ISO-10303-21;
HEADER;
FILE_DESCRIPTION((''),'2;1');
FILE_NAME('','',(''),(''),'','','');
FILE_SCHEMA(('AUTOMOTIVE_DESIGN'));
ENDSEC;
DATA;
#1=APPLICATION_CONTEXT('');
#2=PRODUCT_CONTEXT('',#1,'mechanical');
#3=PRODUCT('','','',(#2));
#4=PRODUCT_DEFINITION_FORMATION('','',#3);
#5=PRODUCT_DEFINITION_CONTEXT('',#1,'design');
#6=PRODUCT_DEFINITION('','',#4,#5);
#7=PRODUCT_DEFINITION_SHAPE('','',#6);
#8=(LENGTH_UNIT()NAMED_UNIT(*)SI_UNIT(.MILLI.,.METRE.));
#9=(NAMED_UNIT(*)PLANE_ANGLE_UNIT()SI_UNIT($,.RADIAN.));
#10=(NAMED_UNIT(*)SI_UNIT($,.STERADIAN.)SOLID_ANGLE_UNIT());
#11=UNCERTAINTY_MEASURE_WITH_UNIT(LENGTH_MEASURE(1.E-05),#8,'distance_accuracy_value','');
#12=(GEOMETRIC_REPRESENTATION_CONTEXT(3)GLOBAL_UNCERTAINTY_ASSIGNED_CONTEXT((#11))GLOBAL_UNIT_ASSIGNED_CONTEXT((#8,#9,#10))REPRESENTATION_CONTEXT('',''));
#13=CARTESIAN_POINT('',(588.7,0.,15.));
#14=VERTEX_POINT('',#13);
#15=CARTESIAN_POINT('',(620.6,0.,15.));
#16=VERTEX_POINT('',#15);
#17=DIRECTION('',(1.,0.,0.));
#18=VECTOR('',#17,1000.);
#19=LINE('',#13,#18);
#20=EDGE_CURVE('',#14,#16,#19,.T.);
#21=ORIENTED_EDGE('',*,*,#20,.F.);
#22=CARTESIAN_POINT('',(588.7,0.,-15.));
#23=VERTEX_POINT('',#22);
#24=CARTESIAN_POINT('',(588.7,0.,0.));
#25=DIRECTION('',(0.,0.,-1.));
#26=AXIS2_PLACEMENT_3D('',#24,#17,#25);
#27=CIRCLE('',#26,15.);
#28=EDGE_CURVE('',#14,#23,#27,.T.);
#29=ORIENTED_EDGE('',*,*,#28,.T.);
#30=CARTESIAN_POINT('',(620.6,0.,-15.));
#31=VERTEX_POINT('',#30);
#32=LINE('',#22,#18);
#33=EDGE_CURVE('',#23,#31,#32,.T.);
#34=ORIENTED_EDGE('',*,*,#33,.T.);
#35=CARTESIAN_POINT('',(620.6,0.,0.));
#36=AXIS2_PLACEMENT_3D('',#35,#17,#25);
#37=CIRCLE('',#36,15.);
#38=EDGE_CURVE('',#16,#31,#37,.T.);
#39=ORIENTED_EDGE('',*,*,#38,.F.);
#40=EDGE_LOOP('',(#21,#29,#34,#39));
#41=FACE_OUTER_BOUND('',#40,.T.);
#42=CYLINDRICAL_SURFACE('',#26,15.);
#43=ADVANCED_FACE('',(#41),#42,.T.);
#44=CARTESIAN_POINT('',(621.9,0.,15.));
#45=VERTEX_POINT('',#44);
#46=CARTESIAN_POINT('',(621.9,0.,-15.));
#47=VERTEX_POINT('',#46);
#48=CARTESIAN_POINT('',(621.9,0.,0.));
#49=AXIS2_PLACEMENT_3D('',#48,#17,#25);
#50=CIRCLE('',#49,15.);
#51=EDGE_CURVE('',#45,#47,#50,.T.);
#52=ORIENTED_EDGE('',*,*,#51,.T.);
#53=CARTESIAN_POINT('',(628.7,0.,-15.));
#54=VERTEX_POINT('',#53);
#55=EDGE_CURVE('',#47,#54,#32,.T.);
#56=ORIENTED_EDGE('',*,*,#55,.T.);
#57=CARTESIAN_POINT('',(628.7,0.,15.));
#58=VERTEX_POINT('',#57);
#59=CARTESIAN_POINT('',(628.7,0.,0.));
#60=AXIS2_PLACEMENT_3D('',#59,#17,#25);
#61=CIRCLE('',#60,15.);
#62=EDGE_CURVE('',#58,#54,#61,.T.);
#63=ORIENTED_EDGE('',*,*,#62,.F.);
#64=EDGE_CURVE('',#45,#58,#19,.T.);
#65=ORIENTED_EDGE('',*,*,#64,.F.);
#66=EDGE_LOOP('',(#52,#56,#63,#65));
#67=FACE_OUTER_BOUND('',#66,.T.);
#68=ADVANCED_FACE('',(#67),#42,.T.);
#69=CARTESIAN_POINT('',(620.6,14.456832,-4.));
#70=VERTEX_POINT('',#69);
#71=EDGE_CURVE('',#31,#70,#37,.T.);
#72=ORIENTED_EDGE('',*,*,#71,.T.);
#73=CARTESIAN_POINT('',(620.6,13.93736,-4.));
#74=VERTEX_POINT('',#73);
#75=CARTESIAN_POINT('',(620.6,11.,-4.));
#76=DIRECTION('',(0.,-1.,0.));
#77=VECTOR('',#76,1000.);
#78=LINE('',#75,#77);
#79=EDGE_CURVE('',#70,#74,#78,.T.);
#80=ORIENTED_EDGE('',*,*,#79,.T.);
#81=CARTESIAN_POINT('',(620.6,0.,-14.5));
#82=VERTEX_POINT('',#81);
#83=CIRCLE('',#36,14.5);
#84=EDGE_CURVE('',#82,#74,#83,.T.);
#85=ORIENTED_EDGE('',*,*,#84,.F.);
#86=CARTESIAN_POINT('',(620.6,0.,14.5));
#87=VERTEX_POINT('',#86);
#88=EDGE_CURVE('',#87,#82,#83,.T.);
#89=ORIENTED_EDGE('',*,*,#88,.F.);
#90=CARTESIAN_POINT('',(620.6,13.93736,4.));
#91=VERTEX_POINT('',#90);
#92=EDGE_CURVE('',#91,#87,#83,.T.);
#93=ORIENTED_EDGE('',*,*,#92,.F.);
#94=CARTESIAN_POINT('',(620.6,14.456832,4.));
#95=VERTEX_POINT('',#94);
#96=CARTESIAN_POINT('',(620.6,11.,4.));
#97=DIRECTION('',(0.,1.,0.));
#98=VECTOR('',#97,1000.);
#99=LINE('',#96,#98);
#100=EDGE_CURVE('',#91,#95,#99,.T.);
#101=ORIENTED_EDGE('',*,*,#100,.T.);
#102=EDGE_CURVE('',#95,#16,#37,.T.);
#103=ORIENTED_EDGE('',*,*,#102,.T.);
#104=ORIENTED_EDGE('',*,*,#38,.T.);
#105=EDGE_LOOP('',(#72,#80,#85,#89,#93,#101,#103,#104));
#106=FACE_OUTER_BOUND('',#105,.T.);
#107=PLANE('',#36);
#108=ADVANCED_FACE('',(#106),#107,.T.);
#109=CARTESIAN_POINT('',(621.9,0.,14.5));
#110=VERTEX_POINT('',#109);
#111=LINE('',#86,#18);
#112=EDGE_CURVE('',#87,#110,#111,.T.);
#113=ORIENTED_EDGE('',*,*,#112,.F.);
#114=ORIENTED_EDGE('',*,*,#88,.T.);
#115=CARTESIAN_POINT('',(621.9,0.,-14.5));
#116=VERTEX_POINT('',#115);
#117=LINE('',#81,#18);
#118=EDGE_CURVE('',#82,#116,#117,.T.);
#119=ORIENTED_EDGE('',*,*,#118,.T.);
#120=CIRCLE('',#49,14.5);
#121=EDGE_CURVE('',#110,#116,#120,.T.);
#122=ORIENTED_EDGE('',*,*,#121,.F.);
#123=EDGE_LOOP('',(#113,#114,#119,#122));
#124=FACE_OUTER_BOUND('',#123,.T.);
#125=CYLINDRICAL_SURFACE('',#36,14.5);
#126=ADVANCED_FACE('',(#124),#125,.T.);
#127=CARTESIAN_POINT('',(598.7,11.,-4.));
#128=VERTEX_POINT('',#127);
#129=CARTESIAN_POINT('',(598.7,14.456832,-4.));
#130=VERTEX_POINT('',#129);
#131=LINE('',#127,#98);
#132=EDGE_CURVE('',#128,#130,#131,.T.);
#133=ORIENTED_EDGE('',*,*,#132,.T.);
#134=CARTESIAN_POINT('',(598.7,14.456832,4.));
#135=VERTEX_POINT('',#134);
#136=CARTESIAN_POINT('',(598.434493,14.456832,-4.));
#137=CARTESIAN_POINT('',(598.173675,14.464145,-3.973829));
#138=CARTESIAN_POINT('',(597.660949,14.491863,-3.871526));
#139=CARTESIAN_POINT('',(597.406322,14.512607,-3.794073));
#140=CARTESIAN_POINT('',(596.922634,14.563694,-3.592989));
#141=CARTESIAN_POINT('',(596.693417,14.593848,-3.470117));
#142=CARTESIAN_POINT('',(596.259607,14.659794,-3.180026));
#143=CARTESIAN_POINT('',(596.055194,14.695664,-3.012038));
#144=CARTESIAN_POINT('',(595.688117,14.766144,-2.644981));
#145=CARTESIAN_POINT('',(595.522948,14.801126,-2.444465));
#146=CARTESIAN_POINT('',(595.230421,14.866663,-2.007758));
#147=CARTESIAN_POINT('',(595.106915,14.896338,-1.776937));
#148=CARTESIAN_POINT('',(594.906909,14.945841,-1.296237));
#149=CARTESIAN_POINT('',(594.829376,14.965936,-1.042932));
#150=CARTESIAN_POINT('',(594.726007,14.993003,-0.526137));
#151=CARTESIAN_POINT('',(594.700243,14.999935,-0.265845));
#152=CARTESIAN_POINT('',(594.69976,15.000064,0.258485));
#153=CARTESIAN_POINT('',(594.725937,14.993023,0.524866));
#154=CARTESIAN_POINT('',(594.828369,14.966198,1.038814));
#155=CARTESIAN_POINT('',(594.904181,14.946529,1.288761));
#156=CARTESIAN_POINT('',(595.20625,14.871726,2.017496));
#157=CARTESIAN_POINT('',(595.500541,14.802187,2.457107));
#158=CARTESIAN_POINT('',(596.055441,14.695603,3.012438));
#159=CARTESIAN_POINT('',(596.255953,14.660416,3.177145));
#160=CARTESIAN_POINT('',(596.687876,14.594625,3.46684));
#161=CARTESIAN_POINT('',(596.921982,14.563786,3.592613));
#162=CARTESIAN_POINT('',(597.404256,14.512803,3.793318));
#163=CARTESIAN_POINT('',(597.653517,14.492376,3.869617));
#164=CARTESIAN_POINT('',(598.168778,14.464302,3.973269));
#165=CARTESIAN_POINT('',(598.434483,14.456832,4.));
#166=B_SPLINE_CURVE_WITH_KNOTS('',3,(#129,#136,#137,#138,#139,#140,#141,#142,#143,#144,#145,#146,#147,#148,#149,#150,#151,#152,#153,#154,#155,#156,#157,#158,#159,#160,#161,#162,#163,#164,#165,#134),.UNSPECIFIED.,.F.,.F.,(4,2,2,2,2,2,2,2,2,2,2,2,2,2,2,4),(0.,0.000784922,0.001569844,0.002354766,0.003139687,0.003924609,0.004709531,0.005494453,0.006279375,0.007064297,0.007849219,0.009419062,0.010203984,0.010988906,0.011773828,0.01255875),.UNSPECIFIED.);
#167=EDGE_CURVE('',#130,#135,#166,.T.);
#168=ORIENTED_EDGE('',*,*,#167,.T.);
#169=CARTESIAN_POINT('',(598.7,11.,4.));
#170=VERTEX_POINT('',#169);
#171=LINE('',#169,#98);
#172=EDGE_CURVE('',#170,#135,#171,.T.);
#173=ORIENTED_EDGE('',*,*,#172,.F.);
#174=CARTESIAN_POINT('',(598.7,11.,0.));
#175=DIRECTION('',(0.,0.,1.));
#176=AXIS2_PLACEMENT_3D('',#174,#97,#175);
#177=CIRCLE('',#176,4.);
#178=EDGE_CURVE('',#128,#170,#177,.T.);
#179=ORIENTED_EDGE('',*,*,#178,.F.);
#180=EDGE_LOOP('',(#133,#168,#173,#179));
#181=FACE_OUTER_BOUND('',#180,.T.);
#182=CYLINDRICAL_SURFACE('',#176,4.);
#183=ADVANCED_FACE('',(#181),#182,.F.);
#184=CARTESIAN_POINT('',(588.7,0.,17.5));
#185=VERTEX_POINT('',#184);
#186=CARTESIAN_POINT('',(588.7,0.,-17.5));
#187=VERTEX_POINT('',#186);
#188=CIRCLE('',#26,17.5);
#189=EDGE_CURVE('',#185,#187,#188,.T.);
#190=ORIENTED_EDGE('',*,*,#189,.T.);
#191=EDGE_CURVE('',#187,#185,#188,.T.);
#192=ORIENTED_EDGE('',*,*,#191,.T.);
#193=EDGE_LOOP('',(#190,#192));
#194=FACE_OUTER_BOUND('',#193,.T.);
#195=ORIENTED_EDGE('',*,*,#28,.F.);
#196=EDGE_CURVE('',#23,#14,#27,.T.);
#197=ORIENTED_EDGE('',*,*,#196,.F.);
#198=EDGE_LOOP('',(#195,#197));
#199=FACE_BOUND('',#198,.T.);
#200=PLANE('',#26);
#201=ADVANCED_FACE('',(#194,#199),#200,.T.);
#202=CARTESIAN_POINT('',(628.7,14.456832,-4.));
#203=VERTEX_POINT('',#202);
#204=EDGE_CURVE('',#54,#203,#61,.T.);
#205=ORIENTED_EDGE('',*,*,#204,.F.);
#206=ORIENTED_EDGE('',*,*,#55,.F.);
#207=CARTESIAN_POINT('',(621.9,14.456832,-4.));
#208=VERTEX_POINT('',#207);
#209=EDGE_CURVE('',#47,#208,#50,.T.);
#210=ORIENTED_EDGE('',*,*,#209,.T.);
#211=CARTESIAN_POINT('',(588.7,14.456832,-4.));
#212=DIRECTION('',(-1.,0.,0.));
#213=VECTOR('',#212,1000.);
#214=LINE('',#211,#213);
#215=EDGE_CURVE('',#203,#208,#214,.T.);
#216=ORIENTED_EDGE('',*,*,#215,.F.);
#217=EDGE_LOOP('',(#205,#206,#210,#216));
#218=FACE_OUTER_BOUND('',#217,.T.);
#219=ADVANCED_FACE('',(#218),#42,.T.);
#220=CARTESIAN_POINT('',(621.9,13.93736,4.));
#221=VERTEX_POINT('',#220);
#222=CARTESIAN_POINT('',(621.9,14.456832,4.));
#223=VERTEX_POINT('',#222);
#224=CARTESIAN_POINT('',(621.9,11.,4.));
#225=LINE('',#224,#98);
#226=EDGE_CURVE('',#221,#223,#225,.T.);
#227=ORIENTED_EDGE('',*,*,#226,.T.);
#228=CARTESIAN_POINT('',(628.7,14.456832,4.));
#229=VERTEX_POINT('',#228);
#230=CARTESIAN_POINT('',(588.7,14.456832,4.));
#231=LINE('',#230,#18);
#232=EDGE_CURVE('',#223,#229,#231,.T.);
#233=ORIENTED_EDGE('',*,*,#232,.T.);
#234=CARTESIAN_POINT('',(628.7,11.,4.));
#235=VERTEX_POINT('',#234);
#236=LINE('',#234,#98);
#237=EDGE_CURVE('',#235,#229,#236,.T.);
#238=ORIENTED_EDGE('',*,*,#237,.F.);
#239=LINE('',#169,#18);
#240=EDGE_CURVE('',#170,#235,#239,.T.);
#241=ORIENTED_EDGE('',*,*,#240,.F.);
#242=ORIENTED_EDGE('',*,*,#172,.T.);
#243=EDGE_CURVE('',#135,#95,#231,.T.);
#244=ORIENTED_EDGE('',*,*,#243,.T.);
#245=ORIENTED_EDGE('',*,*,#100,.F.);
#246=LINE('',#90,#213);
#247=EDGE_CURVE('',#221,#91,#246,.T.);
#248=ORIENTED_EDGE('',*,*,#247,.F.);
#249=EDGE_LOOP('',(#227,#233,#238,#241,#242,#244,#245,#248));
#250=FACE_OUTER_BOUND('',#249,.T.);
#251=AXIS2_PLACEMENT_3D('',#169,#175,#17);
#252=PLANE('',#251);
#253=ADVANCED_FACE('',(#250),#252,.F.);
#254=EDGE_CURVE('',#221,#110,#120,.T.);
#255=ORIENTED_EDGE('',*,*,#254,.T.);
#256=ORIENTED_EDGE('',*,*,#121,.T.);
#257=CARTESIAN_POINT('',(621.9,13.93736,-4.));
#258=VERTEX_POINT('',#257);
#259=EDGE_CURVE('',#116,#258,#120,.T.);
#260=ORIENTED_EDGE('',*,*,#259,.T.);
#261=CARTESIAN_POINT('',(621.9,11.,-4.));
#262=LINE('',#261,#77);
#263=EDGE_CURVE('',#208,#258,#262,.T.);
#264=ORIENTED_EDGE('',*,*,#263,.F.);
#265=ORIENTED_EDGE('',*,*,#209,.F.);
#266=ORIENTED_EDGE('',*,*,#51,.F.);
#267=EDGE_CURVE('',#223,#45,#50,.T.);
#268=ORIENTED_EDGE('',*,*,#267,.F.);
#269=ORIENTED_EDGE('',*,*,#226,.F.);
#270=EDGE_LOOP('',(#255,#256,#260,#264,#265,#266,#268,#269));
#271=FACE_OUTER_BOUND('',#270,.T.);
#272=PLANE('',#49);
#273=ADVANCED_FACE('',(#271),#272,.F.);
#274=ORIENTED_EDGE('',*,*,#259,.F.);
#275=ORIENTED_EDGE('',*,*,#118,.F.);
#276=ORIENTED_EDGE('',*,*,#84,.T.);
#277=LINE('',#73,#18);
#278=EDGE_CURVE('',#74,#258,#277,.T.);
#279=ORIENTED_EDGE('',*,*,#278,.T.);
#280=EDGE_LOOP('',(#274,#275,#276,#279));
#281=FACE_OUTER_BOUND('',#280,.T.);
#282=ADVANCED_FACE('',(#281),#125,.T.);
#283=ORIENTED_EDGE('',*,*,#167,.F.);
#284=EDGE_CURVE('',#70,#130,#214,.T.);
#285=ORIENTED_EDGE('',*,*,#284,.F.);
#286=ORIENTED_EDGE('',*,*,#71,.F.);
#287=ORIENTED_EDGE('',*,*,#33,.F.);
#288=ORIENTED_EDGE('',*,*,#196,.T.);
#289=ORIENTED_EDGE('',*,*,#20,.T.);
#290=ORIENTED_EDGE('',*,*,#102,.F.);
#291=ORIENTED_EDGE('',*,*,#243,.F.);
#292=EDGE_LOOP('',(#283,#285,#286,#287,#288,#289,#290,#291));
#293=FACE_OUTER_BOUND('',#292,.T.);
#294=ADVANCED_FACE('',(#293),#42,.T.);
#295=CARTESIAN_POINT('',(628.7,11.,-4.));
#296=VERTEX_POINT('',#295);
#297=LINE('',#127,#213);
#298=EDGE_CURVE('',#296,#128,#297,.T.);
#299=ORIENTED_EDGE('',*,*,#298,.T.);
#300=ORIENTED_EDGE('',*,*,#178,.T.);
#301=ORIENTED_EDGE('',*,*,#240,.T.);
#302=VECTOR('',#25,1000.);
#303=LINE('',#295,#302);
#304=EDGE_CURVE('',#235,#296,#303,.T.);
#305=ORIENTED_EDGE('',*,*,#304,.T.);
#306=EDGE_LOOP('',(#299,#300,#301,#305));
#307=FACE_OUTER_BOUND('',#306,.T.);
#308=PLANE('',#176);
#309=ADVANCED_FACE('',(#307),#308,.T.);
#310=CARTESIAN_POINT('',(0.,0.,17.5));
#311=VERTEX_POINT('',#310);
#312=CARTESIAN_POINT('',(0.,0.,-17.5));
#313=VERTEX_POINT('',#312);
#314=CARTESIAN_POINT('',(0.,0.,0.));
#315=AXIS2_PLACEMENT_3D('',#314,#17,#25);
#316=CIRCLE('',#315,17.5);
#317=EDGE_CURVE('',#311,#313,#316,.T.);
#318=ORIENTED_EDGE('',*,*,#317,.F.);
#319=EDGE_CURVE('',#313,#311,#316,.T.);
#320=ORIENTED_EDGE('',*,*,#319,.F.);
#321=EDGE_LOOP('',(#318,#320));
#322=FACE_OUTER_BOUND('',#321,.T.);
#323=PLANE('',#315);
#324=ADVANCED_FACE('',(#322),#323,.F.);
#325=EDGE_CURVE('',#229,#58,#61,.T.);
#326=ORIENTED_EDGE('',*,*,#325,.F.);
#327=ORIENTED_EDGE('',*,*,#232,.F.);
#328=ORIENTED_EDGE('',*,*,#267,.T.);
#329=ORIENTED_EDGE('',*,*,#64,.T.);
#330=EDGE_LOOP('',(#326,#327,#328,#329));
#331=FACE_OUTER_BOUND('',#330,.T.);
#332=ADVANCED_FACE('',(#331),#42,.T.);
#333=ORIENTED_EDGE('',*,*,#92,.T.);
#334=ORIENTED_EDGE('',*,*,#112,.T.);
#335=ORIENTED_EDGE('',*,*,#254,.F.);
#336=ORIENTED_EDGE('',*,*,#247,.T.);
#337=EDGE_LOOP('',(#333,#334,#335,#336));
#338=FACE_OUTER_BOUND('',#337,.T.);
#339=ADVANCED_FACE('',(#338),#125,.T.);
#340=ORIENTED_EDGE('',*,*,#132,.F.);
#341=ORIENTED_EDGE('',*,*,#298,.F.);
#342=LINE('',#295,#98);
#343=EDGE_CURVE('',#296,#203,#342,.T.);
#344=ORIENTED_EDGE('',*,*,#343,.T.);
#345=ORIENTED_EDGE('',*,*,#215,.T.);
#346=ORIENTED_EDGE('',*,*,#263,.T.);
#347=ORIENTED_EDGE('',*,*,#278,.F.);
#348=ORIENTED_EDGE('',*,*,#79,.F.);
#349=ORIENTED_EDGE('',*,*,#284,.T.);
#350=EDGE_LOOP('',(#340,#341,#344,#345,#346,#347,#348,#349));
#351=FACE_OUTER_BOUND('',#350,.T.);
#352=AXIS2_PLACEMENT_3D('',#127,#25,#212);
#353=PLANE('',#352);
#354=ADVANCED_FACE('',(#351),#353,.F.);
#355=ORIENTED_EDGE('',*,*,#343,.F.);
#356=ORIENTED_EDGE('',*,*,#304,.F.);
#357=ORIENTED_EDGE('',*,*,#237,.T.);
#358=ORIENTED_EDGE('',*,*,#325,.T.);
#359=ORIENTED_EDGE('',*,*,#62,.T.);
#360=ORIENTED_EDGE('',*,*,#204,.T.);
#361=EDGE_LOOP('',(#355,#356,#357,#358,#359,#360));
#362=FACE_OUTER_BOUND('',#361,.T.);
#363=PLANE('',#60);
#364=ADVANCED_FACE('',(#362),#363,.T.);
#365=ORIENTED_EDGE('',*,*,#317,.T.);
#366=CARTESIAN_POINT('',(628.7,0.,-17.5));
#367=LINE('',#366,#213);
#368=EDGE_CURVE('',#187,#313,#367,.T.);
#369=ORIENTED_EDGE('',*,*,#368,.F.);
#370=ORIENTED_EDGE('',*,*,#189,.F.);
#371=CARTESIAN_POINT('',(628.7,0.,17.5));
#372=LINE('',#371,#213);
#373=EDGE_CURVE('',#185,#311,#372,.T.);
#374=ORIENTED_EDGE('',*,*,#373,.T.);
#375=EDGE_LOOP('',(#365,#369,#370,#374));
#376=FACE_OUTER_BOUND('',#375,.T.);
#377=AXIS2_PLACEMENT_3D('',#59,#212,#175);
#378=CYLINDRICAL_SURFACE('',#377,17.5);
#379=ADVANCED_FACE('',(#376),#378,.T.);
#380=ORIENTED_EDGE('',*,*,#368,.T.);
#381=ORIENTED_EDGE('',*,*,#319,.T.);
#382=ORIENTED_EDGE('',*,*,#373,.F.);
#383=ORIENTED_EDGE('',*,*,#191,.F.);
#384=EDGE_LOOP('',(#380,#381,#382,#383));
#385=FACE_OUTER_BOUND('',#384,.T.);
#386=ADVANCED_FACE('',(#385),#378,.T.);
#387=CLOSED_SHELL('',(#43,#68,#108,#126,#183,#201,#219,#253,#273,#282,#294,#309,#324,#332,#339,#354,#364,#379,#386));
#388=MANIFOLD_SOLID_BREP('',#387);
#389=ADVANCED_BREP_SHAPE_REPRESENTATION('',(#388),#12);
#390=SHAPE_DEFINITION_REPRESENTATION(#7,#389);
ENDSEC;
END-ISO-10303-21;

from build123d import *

# Parameters (mm, degrees)
SKETCH_1_R          = 17.5
EXTRUDE_1_DEPTH     = 628.7
CUT_EXTRUDE_START   = -40
SKETCH_3_R          = 17.5
SKETCH_3_R_2        = 15
CUT_EXTRUDE_1_DEPTH = 40
CUT_EXTRUDE_2_DEPTH = 4
CUT_EXTRUDE_START_2 = 31.9
SKETCH_5_R          = 15
SKETCH_5_R_2        = 14.5
CUT_EXTRUDE_3_DEPTH = 1.3


with BuildPart() as part:
    # 草图1 → 凸台-拉伸1 (new body)
    with BuildSketch(Plane(origin=(0, 0, 0), x_dir=(0, 0, -1), z_dir=(1, 0, 0))):
        with Locations(Location((0, 0, 0), (0, 0, 180))):
            Circle(SKETCH_1_R)
    extrude(amount=EXTRUDE_1_DEPTH)

    # 草图3 → 切除-拉伸1 (cut)
    with BuildSketch(Plane(origin=(628.7, 0, 0), x_dir=(0, 0, -1), z_dir=(1, 0, 0)).offset(CUT_EXTRUDE_START)):
        with Locations(Location((0, 0, 0), (0, 0, 180))):
            Circle(SKETCH_3_R)
        Circle(SKETCH_3_R_2, mode=Mode.SUBTRACT)
    extrude(amount=CUT_EXTRUDE_1_DEPTH, mode=Mode.SUBTRACT)

    # 草图4 → 切除-拉伸2 (cut)
    with BuildSketch(Plane(origin=(0, 15, 0), x_dir=(1, 0, 0), z_dir=(0, 1, 0))):
        with BuildLine():
            Line((598.7, 4), (628.7, 4))
            Line((628.7, 4), (628.7, -4))
            Line((628.7, -4), (598.7, -4))
            ThreePointArc((598.7, -4), (594.7, 0), (598.7, 4))
        make_face()
    extrude(amount=-CUT_EXTRUDE_2_DEPTH, mode=Mode.SUBTRACT)

    # 草图5 → 切除-拉伸3 (cut)
    with BuildSketch(Plane(origin=(588.7, 0, 0), x_dir=(0, 0, -1), z_dir=(1, 0, 0)).offset(CUT_EXTRUDE_START_2)):
        Circle(SKETCH_5_R)
        Circle(SKETCH_5_R_2, mode=Mode.SUBTRACT)
    extrude(amount=CUT_EXTRUDE_3_DEPTH, mode=Mode.SUBTRACT)


solid = part.part
